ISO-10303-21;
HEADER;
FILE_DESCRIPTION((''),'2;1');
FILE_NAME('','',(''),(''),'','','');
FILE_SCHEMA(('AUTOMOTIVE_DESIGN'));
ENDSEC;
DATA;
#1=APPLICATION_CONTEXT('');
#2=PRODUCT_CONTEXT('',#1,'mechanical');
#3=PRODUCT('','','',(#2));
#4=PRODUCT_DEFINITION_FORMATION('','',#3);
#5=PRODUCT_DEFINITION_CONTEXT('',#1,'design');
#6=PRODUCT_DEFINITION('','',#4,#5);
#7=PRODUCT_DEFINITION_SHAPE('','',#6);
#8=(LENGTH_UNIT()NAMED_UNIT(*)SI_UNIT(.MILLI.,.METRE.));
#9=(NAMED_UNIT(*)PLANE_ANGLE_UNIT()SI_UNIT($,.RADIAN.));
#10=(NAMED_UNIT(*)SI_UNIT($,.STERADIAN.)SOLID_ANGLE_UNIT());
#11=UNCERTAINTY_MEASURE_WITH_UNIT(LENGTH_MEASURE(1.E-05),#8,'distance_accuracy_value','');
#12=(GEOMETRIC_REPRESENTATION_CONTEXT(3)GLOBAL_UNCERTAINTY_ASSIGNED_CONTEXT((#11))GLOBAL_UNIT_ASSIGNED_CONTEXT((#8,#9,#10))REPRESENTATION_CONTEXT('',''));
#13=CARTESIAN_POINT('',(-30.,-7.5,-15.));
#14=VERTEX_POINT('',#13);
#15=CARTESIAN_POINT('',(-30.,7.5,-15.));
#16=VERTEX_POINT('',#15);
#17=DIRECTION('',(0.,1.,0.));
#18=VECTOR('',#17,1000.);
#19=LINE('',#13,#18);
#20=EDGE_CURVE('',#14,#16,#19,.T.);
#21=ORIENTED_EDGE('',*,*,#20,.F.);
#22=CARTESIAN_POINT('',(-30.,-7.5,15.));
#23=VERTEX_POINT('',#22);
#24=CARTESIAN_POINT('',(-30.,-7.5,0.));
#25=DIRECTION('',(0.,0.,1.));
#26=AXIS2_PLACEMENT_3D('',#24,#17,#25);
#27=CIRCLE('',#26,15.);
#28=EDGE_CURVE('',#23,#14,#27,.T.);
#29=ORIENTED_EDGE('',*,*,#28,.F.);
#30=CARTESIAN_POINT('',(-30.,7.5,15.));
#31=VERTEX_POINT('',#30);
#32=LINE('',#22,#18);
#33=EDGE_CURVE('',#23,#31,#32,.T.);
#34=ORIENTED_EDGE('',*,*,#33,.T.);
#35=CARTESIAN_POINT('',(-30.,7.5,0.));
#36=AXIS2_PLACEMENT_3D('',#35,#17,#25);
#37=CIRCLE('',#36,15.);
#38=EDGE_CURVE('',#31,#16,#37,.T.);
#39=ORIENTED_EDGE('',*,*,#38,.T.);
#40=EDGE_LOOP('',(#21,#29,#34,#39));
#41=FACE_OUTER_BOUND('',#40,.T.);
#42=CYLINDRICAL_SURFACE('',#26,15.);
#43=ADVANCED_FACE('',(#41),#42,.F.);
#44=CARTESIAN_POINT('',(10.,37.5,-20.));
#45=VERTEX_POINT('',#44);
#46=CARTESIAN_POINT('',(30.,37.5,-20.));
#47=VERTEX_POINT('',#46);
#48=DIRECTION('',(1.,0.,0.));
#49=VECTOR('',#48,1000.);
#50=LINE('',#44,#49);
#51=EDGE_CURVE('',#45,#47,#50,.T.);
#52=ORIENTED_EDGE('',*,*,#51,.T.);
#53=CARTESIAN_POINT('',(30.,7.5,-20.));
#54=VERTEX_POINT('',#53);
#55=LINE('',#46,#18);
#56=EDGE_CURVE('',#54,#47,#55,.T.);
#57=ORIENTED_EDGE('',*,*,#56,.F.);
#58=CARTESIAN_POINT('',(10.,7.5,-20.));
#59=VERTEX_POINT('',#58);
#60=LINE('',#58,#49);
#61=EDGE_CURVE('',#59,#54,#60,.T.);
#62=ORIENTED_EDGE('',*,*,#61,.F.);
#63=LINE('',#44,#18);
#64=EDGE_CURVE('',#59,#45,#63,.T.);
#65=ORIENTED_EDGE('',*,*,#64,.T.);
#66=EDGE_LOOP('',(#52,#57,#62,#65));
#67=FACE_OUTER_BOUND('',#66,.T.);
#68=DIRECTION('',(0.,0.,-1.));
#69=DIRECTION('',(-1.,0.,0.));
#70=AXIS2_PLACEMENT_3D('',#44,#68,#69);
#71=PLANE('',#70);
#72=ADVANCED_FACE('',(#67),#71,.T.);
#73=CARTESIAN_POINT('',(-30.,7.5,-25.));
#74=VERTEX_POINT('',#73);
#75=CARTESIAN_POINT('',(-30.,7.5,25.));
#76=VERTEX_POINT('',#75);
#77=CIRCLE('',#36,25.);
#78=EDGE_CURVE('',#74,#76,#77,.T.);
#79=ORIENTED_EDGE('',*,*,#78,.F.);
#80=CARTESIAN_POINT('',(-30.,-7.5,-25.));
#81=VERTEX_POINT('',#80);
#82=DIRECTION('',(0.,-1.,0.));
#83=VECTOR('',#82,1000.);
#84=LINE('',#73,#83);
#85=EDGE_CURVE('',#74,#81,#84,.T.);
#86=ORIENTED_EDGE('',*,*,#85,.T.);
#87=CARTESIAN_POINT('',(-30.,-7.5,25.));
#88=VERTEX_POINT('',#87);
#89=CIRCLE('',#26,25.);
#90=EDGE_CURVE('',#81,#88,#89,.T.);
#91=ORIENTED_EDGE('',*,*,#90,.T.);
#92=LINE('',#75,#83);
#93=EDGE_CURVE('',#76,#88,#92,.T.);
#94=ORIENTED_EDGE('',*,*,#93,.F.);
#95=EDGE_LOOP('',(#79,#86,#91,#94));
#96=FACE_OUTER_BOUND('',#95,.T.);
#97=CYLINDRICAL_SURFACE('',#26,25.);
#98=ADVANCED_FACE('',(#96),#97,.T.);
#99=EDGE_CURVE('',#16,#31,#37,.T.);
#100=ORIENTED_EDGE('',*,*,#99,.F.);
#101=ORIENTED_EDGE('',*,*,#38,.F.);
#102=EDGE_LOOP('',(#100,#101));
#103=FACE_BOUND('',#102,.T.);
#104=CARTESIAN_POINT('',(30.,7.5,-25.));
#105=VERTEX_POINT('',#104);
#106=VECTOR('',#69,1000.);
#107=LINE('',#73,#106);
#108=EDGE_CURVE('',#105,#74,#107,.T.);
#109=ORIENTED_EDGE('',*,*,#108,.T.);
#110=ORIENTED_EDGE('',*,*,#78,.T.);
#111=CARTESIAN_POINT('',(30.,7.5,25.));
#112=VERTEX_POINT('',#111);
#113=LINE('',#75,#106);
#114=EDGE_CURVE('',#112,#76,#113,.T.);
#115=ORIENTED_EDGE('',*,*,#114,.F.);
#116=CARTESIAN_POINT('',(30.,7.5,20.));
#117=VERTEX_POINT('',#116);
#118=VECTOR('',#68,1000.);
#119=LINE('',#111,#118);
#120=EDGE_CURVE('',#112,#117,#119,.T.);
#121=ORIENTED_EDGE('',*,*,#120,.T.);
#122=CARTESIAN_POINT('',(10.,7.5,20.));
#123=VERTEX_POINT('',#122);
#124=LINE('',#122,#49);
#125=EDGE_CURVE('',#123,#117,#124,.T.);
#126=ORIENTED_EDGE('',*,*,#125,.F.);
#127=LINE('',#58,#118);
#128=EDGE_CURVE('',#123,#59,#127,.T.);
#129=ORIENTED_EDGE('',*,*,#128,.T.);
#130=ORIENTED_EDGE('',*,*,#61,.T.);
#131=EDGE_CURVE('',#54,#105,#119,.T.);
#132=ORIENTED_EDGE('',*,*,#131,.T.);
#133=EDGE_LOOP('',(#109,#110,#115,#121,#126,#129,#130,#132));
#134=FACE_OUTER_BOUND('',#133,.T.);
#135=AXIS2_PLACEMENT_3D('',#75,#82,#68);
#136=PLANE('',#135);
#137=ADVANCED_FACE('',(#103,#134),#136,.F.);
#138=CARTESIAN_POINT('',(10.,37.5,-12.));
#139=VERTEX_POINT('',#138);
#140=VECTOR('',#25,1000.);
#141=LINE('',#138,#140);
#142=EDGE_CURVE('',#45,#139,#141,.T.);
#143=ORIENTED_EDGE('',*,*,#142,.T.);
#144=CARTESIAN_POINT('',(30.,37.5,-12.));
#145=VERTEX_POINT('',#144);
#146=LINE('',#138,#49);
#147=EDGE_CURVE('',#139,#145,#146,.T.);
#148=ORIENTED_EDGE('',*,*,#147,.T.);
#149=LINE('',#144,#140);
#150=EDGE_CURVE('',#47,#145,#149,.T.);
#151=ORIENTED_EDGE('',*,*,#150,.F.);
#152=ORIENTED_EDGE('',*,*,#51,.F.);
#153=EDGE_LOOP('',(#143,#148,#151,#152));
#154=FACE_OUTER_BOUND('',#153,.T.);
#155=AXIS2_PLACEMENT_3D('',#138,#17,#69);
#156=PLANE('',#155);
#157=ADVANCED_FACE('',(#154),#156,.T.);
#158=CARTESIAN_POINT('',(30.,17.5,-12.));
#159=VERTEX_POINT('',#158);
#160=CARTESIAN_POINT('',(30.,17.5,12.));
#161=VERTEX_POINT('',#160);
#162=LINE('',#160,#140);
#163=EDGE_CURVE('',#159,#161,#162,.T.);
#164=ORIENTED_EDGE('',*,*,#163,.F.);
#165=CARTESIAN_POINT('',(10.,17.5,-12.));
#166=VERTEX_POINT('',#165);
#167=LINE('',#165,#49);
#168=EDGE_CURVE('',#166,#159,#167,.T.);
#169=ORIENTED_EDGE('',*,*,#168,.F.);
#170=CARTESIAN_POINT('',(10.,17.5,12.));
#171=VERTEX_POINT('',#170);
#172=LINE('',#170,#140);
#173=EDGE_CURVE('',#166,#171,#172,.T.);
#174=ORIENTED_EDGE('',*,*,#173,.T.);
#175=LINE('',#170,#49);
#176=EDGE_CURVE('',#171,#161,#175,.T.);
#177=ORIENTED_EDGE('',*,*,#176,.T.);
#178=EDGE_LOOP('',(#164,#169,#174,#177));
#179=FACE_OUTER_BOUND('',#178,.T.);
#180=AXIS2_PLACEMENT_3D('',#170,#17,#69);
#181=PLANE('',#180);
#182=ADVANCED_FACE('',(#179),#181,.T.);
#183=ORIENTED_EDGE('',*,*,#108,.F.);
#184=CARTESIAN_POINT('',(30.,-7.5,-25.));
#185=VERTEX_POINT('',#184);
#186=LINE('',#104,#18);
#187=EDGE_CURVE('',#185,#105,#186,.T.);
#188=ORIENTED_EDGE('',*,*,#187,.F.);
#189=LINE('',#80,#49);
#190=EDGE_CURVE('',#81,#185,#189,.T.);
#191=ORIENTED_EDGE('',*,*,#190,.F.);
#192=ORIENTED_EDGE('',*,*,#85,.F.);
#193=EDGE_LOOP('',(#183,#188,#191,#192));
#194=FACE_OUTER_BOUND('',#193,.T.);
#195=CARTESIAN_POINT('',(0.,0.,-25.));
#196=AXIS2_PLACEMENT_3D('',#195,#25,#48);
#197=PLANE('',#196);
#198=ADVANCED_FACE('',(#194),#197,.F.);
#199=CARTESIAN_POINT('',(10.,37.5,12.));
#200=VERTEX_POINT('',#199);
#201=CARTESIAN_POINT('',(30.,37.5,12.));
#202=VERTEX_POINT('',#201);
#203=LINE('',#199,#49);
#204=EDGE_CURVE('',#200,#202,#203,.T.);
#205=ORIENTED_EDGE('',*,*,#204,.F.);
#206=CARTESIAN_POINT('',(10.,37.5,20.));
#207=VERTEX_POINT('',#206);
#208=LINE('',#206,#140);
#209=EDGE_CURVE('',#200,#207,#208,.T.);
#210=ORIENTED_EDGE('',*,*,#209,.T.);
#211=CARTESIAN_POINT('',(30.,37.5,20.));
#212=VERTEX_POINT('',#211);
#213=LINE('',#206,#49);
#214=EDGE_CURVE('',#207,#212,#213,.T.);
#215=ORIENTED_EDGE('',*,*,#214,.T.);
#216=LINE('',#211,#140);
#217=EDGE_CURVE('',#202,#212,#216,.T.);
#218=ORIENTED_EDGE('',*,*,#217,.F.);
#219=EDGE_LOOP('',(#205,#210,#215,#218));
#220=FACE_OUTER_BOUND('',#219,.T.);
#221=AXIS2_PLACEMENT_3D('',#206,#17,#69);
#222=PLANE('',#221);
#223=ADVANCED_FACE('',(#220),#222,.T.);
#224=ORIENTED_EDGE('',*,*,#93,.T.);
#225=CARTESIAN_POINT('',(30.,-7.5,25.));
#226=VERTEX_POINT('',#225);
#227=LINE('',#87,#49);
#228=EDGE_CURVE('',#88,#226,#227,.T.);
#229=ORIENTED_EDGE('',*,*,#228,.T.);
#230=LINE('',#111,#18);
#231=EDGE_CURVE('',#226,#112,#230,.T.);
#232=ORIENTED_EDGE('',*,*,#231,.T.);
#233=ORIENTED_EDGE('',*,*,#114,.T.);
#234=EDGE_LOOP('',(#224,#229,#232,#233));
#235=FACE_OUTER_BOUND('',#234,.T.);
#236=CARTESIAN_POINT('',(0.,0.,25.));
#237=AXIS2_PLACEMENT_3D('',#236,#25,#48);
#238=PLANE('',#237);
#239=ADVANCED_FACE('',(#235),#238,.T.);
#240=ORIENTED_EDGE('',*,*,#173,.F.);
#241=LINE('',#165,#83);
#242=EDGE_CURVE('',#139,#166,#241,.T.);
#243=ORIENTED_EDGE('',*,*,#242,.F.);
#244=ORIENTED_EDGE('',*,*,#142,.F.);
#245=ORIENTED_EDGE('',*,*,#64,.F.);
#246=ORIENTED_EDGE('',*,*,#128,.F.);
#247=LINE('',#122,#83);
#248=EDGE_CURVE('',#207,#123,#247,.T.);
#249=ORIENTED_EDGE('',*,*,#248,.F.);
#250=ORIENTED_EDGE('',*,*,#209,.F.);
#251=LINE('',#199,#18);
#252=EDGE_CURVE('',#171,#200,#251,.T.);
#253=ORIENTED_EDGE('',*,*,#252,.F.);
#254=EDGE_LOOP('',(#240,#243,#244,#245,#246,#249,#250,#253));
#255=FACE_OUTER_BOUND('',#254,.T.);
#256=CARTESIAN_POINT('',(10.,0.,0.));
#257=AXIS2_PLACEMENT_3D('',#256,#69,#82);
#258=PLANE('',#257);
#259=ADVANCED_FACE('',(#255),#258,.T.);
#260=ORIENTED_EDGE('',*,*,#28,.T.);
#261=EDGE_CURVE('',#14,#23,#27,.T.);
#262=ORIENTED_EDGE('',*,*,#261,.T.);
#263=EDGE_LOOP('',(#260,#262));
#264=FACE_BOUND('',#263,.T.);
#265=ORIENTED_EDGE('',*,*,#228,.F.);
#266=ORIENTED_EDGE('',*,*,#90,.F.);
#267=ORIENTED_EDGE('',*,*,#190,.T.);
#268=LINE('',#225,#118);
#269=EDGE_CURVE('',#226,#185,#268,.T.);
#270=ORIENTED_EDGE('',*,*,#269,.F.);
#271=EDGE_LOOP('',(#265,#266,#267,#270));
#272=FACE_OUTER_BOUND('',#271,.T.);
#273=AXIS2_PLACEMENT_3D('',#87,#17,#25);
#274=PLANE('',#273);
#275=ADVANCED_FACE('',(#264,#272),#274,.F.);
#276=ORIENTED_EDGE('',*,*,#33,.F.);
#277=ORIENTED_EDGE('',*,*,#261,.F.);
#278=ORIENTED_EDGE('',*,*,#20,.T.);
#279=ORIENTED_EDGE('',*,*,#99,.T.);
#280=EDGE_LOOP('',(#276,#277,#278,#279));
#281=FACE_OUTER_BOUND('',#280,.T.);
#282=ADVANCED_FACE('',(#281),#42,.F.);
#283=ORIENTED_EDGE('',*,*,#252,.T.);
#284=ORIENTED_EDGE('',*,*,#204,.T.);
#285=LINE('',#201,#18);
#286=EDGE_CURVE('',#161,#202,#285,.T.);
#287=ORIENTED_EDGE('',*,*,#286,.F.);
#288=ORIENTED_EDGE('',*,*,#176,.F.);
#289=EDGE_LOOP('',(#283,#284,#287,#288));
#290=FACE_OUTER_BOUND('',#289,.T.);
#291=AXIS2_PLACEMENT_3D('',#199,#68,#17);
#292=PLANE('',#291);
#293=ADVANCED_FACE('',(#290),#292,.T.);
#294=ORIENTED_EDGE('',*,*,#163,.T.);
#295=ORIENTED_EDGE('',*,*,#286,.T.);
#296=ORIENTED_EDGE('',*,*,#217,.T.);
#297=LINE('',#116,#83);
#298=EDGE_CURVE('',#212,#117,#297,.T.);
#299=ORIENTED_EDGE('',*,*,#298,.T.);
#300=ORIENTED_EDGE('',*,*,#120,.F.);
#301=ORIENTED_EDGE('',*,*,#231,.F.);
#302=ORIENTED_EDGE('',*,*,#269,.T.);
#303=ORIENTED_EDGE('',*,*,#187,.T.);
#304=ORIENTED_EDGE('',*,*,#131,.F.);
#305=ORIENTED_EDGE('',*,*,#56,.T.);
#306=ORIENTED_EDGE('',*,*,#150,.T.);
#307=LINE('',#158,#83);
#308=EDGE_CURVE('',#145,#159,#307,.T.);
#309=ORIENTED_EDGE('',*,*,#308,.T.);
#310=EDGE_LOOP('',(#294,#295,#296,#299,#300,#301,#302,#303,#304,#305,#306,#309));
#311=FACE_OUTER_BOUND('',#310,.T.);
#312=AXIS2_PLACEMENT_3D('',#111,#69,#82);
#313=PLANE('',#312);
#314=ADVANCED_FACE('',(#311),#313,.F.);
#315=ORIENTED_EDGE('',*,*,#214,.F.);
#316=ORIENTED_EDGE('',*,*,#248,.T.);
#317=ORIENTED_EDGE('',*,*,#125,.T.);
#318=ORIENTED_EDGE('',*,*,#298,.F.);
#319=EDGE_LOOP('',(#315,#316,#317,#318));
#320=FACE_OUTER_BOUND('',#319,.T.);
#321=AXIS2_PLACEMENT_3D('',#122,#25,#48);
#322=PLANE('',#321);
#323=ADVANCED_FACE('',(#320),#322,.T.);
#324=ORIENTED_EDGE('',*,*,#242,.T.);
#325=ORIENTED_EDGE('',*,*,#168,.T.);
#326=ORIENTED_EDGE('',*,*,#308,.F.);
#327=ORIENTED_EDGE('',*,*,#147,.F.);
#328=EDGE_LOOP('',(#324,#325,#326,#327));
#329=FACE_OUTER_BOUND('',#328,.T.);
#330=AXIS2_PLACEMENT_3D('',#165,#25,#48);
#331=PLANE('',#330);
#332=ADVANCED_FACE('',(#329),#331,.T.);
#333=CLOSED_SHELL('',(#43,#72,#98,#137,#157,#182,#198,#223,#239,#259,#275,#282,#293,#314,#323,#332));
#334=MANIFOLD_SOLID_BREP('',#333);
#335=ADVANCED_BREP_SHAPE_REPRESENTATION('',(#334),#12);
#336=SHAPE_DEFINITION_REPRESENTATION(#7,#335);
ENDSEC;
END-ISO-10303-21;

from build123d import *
from build123d.topology import SkipClean

# Parameters (mm, degrees)
BASE_BLOCK_SKETCH_W   = 60
BASE_BLOCK_SKETCH_H   = 15
BASE_BLOCK_DEPTH      = 25
FORK_UPRIGHT_DEPTH    = 20
ROUNDED_END_LUG_DEPTH = 15
BORE_SKETCH_R         = 15
BORE_30_DEPTH         = 15


with BuildPart() as part:
    # Base Block Sketch → Base Block (new, symmetric)
    with BuildSketch(Plane.XY):
        Rectangle(BASE_BLOCK_SKETCH_W, BASE_BLOCK_SKETCH_H)
    extrude(amount=BASE_BLOCK_DEPTH, both=True)

    # Fork Upright Sketch → Fork Upright (add)
    with BuildSketch(Plane(origin=(30, 0, 0), x_dir=(0, 0, -1), z_dir=(1, 0, 0))):
        Polygon((-20, 7.5), (-20, 37.5), (-12, 37.5), (-12, 17.5), (12, 17.5), (12, 37.5), (20, 37.5), (20, 7.5), align=None)
    extrude(amount=-FORK_UPRIGHT_DEPTH)

    # End Lug Sketch → Rounded End Lug (add)
    with BuildSketch(Plane(origin=(0, 7.5, 0), x_dir=(1, 0, 0), z_dir=(0, 1, 0))):
        with BuildLine():
            Line((-30, 15), (-30, 25))
            ThreePointArc((-30, 25), (-55, 0), (-30, -25))
            Line((-30, -25), (-30, -15))
            ThreePointArc((-30, -15), (-45, 0), (-30, 15))
        make_face()
    extrude(amount=-ROUNDED_END_LUG_DEPTH)

    # Bore Sketch → Bore Ø30 (cut)
    with SkipClean():  # the faces are left unmerged after this step: merging them gives an invalid solid
        with BuildSketch(Plane(origin=(0, 7.5, 0), x_dir=(1, 0, 0), z_dir=(0, 1, 0))):
            with Locations(Location((-30, 0, 0), (0, 0, 270))):
                Circle(BORE_SKETCH_R)
        extrude(amount=-BORE_30_DEPTH, mode=Mode.SUBTRACT)


solid = part.part
